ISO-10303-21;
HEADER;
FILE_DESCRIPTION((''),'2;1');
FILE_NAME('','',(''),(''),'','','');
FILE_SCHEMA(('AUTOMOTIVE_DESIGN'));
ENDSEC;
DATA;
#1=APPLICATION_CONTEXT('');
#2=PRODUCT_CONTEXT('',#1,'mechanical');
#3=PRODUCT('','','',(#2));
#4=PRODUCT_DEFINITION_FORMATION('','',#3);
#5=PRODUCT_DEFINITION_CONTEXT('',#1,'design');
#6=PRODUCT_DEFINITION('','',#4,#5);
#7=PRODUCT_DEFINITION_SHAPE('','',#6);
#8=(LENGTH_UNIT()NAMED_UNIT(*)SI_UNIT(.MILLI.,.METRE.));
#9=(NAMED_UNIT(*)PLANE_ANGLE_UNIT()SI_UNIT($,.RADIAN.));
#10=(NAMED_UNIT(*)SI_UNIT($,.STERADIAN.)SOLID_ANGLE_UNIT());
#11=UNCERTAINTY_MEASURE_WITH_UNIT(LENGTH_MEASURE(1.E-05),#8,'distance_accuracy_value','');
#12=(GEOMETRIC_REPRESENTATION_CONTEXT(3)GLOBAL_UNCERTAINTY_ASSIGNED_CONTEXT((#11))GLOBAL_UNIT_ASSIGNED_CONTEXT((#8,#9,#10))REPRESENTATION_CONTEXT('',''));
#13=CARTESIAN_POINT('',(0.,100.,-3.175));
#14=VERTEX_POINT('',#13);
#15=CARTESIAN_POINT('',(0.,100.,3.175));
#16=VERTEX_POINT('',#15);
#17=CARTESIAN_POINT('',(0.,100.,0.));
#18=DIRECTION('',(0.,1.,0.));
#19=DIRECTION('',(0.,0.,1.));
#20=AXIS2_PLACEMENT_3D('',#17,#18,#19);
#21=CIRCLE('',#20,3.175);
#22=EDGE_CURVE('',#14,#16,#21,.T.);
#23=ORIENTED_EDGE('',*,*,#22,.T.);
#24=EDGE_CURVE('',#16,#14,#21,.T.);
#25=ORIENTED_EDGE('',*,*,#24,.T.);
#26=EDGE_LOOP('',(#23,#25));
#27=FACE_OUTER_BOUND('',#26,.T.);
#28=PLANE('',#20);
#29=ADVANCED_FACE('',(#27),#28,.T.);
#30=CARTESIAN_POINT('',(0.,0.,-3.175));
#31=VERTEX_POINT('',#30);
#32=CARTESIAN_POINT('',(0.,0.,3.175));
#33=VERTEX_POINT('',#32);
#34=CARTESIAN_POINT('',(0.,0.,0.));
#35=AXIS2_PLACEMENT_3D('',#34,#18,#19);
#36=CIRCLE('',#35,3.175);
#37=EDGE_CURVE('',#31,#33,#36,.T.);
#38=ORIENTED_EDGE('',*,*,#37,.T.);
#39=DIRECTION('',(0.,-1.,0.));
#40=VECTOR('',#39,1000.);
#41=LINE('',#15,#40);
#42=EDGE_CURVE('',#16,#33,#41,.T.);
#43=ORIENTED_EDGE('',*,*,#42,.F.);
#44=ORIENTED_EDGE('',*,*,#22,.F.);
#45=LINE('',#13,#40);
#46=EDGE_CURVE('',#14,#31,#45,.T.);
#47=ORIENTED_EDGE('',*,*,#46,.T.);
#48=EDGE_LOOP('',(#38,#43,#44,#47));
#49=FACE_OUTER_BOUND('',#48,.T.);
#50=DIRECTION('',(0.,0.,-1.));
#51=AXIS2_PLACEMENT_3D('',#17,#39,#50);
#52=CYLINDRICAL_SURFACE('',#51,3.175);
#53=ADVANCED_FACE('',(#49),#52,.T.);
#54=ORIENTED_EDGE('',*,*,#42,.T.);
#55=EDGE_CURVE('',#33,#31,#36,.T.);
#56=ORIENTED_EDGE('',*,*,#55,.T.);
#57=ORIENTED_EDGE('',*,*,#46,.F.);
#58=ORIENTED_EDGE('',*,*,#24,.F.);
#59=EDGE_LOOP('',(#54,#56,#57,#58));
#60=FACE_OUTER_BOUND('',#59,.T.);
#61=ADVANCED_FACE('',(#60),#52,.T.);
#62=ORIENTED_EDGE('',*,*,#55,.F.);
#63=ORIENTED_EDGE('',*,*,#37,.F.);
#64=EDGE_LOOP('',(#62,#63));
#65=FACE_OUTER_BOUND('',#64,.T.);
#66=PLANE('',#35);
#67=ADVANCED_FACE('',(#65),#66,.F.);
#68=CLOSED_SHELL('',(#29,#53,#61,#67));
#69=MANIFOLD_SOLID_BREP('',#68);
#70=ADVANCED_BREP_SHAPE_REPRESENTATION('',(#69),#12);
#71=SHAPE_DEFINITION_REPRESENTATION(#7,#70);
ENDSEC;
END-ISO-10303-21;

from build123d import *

# Parameters (mm, degrees)
SKETCH1_R           = 3.175
BOSS_EXTRUDE1_DEPTH = 100


with BuildPart() as part:
    # Sketch1 → Boss-Extrude1 (new body)
    with BuildSketch(Plane(origin=(0, 0, 0), x_dir=(1, 0, 0), z_dir=(0, 1, 0))):
        with Locations(Location((0, 0, 0), (0, 0, 270))):
            Circle(SKETCH1_R)
    extrude(amount=BOSS_EXTRUDE1_DEPTH)


solid = part.part
